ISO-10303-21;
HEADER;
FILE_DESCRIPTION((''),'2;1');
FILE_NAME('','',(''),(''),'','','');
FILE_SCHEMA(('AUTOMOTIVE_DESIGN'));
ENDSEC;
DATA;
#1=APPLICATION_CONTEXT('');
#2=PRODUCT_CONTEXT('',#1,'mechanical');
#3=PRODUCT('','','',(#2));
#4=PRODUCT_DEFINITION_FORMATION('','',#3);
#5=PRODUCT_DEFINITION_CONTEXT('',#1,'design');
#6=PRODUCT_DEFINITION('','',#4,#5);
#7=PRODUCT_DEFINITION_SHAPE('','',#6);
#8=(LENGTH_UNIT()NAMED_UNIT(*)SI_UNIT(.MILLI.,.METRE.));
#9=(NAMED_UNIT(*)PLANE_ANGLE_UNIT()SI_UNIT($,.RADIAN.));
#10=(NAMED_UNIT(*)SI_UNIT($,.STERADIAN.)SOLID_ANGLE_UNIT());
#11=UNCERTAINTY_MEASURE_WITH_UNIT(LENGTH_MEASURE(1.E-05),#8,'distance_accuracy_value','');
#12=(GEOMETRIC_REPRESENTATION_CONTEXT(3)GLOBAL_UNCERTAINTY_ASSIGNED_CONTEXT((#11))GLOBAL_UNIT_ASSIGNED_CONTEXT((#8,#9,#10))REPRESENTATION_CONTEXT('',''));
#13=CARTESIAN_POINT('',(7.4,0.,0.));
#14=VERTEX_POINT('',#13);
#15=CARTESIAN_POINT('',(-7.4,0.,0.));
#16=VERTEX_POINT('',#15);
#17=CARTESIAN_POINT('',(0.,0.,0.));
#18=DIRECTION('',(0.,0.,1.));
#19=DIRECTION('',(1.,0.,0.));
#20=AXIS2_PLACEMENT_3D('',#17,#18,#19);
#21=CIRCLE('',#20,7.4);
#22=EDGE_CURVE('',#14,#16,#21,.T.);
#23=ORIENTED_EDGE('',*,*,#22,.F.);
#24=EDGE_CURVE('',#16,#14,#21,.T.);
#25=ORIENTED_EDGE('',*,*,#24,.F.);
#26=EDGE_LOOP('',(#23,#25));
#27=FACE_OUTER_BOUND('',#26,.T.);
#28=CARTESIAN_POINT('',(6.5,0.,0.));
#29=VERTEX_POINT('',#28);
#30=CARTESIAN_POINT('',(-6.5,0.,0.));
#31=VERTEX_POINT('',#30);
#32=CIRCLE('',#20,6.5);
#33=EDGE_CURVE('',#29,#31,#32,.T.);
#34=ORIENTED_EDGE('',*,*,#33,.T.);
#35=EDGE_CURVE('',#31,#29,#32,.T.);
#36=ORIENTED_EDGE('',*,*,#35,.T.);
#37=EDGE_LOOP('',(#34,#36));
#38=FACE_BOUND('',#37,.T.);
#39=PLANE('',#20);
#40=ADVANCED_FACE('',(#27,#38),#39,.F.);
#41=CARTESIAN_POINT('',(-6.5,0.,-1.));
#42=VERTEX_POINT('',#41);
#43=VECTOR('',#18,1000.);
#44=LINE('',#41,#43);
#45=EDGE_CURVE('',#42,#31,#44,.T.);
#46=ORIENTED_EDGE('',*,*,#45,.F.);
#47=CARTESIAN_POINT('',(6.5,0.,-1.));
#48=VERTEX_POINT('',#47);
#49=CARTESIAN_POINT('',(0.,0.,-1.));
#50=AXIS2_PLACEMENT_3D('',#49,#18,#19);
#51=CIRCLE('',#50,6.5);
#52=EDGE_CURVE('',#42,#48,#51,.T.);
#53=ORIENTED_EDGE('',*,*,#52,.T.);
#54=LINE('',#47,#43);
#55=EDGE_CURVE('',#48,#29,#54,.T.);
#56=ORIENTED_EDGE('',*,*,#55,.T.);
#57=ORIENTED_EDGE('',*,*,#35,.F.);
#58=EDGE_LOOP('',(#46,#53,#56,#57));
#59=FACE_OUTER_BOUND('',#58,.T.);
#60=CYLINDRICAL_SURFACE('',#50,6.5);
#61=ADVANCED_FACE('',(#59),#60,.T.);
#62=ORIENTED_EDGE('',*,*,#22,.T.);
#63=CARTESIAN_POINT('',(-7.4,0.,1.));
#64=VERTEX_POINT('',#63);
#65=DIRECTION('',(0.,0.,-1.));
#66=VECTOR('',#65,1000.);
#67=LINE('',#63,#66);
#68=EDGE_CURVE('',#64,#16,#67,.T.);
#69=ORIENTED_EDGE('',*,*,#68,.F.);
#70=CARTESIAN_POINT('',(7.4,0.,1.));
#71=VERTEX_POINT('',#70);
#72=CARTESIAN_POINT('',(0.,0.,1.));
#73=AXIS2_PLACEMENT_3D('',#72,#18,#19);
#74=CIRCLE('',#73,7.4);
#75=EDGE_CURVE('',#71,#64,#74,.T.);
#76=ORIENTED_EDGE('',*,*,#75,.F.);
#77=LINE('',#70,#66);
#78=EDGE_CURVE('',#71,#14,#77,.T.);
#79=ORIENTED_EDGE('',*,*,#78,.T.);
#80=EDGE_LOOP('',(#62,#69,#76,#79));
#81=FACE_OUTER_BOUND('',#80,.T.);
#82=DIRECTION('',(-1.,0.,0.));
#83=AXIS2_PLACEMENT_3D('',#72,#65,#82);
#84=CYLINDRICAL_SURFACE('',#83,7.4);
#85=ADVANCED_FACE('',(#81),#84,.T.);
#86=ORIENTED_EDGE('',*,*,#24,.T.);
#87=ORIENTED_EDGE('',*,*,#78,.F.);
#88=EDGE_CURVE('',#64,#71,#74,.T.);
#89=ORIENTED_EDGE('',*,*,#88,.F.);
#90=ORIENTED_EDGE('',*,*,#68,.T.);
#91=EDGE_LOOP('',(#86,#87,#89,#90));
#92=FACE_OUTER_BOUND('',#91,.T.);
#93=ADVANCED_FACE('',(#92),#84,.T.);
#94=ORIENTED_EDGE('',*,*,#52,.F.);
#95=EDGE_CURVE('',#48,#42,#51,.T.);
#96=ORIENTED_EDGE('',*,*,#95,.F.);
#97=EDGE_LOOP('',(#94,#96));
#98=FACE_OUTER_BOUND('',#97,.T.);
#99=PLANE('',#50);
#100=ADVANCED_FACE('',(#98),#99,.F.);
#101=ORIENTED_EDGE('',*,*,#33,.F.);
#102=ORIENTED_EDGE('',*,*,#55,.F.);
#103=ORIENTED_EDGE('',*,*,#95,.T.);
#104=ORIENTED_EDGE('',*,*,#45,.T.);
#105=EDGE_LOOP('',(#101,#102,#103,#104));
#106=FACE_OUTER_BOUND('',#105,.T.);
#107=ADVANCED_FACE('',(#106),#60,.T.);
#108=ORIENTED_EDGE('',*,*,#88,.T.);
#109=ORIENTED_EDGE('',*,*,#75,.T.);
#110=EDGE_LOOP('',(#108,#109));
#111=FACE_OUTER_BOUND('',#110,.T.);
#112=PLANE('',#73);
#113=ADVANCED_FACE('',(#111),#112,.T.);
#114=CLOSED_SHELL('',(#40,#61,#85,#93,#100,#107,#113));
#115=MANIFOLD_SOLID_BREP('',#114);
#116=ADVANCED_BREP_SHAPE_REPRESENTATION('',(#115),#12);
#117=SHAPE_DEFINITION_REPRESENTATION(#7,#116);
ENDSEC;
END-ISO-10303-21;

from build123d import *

# Parameters (mm, degrees)
SKETCH_1_R      = 7.4
EXTRUDE_1_DEPTH = 1
SKETCH_1_3_R    = 6.5
EXTRUDE_2_DEPTH = 1


with BuildPart() as part:
    # 草图1 → 凸台-拉伸1 (new body)
    with BuildSketch(Plane.XY):
        Circle(SKETCH_1_R)
    extrude(amount=EXTRUDE_1_DEPTH)

    # 草图1<3> → 凸台-拉伸2 (add)
    with BuildSketch(Plane.XY):
        Circle(SKETCH_1_3_R)
    extrude(amount=-EXTRUDE_2_DEPTH)


solid = part.part
